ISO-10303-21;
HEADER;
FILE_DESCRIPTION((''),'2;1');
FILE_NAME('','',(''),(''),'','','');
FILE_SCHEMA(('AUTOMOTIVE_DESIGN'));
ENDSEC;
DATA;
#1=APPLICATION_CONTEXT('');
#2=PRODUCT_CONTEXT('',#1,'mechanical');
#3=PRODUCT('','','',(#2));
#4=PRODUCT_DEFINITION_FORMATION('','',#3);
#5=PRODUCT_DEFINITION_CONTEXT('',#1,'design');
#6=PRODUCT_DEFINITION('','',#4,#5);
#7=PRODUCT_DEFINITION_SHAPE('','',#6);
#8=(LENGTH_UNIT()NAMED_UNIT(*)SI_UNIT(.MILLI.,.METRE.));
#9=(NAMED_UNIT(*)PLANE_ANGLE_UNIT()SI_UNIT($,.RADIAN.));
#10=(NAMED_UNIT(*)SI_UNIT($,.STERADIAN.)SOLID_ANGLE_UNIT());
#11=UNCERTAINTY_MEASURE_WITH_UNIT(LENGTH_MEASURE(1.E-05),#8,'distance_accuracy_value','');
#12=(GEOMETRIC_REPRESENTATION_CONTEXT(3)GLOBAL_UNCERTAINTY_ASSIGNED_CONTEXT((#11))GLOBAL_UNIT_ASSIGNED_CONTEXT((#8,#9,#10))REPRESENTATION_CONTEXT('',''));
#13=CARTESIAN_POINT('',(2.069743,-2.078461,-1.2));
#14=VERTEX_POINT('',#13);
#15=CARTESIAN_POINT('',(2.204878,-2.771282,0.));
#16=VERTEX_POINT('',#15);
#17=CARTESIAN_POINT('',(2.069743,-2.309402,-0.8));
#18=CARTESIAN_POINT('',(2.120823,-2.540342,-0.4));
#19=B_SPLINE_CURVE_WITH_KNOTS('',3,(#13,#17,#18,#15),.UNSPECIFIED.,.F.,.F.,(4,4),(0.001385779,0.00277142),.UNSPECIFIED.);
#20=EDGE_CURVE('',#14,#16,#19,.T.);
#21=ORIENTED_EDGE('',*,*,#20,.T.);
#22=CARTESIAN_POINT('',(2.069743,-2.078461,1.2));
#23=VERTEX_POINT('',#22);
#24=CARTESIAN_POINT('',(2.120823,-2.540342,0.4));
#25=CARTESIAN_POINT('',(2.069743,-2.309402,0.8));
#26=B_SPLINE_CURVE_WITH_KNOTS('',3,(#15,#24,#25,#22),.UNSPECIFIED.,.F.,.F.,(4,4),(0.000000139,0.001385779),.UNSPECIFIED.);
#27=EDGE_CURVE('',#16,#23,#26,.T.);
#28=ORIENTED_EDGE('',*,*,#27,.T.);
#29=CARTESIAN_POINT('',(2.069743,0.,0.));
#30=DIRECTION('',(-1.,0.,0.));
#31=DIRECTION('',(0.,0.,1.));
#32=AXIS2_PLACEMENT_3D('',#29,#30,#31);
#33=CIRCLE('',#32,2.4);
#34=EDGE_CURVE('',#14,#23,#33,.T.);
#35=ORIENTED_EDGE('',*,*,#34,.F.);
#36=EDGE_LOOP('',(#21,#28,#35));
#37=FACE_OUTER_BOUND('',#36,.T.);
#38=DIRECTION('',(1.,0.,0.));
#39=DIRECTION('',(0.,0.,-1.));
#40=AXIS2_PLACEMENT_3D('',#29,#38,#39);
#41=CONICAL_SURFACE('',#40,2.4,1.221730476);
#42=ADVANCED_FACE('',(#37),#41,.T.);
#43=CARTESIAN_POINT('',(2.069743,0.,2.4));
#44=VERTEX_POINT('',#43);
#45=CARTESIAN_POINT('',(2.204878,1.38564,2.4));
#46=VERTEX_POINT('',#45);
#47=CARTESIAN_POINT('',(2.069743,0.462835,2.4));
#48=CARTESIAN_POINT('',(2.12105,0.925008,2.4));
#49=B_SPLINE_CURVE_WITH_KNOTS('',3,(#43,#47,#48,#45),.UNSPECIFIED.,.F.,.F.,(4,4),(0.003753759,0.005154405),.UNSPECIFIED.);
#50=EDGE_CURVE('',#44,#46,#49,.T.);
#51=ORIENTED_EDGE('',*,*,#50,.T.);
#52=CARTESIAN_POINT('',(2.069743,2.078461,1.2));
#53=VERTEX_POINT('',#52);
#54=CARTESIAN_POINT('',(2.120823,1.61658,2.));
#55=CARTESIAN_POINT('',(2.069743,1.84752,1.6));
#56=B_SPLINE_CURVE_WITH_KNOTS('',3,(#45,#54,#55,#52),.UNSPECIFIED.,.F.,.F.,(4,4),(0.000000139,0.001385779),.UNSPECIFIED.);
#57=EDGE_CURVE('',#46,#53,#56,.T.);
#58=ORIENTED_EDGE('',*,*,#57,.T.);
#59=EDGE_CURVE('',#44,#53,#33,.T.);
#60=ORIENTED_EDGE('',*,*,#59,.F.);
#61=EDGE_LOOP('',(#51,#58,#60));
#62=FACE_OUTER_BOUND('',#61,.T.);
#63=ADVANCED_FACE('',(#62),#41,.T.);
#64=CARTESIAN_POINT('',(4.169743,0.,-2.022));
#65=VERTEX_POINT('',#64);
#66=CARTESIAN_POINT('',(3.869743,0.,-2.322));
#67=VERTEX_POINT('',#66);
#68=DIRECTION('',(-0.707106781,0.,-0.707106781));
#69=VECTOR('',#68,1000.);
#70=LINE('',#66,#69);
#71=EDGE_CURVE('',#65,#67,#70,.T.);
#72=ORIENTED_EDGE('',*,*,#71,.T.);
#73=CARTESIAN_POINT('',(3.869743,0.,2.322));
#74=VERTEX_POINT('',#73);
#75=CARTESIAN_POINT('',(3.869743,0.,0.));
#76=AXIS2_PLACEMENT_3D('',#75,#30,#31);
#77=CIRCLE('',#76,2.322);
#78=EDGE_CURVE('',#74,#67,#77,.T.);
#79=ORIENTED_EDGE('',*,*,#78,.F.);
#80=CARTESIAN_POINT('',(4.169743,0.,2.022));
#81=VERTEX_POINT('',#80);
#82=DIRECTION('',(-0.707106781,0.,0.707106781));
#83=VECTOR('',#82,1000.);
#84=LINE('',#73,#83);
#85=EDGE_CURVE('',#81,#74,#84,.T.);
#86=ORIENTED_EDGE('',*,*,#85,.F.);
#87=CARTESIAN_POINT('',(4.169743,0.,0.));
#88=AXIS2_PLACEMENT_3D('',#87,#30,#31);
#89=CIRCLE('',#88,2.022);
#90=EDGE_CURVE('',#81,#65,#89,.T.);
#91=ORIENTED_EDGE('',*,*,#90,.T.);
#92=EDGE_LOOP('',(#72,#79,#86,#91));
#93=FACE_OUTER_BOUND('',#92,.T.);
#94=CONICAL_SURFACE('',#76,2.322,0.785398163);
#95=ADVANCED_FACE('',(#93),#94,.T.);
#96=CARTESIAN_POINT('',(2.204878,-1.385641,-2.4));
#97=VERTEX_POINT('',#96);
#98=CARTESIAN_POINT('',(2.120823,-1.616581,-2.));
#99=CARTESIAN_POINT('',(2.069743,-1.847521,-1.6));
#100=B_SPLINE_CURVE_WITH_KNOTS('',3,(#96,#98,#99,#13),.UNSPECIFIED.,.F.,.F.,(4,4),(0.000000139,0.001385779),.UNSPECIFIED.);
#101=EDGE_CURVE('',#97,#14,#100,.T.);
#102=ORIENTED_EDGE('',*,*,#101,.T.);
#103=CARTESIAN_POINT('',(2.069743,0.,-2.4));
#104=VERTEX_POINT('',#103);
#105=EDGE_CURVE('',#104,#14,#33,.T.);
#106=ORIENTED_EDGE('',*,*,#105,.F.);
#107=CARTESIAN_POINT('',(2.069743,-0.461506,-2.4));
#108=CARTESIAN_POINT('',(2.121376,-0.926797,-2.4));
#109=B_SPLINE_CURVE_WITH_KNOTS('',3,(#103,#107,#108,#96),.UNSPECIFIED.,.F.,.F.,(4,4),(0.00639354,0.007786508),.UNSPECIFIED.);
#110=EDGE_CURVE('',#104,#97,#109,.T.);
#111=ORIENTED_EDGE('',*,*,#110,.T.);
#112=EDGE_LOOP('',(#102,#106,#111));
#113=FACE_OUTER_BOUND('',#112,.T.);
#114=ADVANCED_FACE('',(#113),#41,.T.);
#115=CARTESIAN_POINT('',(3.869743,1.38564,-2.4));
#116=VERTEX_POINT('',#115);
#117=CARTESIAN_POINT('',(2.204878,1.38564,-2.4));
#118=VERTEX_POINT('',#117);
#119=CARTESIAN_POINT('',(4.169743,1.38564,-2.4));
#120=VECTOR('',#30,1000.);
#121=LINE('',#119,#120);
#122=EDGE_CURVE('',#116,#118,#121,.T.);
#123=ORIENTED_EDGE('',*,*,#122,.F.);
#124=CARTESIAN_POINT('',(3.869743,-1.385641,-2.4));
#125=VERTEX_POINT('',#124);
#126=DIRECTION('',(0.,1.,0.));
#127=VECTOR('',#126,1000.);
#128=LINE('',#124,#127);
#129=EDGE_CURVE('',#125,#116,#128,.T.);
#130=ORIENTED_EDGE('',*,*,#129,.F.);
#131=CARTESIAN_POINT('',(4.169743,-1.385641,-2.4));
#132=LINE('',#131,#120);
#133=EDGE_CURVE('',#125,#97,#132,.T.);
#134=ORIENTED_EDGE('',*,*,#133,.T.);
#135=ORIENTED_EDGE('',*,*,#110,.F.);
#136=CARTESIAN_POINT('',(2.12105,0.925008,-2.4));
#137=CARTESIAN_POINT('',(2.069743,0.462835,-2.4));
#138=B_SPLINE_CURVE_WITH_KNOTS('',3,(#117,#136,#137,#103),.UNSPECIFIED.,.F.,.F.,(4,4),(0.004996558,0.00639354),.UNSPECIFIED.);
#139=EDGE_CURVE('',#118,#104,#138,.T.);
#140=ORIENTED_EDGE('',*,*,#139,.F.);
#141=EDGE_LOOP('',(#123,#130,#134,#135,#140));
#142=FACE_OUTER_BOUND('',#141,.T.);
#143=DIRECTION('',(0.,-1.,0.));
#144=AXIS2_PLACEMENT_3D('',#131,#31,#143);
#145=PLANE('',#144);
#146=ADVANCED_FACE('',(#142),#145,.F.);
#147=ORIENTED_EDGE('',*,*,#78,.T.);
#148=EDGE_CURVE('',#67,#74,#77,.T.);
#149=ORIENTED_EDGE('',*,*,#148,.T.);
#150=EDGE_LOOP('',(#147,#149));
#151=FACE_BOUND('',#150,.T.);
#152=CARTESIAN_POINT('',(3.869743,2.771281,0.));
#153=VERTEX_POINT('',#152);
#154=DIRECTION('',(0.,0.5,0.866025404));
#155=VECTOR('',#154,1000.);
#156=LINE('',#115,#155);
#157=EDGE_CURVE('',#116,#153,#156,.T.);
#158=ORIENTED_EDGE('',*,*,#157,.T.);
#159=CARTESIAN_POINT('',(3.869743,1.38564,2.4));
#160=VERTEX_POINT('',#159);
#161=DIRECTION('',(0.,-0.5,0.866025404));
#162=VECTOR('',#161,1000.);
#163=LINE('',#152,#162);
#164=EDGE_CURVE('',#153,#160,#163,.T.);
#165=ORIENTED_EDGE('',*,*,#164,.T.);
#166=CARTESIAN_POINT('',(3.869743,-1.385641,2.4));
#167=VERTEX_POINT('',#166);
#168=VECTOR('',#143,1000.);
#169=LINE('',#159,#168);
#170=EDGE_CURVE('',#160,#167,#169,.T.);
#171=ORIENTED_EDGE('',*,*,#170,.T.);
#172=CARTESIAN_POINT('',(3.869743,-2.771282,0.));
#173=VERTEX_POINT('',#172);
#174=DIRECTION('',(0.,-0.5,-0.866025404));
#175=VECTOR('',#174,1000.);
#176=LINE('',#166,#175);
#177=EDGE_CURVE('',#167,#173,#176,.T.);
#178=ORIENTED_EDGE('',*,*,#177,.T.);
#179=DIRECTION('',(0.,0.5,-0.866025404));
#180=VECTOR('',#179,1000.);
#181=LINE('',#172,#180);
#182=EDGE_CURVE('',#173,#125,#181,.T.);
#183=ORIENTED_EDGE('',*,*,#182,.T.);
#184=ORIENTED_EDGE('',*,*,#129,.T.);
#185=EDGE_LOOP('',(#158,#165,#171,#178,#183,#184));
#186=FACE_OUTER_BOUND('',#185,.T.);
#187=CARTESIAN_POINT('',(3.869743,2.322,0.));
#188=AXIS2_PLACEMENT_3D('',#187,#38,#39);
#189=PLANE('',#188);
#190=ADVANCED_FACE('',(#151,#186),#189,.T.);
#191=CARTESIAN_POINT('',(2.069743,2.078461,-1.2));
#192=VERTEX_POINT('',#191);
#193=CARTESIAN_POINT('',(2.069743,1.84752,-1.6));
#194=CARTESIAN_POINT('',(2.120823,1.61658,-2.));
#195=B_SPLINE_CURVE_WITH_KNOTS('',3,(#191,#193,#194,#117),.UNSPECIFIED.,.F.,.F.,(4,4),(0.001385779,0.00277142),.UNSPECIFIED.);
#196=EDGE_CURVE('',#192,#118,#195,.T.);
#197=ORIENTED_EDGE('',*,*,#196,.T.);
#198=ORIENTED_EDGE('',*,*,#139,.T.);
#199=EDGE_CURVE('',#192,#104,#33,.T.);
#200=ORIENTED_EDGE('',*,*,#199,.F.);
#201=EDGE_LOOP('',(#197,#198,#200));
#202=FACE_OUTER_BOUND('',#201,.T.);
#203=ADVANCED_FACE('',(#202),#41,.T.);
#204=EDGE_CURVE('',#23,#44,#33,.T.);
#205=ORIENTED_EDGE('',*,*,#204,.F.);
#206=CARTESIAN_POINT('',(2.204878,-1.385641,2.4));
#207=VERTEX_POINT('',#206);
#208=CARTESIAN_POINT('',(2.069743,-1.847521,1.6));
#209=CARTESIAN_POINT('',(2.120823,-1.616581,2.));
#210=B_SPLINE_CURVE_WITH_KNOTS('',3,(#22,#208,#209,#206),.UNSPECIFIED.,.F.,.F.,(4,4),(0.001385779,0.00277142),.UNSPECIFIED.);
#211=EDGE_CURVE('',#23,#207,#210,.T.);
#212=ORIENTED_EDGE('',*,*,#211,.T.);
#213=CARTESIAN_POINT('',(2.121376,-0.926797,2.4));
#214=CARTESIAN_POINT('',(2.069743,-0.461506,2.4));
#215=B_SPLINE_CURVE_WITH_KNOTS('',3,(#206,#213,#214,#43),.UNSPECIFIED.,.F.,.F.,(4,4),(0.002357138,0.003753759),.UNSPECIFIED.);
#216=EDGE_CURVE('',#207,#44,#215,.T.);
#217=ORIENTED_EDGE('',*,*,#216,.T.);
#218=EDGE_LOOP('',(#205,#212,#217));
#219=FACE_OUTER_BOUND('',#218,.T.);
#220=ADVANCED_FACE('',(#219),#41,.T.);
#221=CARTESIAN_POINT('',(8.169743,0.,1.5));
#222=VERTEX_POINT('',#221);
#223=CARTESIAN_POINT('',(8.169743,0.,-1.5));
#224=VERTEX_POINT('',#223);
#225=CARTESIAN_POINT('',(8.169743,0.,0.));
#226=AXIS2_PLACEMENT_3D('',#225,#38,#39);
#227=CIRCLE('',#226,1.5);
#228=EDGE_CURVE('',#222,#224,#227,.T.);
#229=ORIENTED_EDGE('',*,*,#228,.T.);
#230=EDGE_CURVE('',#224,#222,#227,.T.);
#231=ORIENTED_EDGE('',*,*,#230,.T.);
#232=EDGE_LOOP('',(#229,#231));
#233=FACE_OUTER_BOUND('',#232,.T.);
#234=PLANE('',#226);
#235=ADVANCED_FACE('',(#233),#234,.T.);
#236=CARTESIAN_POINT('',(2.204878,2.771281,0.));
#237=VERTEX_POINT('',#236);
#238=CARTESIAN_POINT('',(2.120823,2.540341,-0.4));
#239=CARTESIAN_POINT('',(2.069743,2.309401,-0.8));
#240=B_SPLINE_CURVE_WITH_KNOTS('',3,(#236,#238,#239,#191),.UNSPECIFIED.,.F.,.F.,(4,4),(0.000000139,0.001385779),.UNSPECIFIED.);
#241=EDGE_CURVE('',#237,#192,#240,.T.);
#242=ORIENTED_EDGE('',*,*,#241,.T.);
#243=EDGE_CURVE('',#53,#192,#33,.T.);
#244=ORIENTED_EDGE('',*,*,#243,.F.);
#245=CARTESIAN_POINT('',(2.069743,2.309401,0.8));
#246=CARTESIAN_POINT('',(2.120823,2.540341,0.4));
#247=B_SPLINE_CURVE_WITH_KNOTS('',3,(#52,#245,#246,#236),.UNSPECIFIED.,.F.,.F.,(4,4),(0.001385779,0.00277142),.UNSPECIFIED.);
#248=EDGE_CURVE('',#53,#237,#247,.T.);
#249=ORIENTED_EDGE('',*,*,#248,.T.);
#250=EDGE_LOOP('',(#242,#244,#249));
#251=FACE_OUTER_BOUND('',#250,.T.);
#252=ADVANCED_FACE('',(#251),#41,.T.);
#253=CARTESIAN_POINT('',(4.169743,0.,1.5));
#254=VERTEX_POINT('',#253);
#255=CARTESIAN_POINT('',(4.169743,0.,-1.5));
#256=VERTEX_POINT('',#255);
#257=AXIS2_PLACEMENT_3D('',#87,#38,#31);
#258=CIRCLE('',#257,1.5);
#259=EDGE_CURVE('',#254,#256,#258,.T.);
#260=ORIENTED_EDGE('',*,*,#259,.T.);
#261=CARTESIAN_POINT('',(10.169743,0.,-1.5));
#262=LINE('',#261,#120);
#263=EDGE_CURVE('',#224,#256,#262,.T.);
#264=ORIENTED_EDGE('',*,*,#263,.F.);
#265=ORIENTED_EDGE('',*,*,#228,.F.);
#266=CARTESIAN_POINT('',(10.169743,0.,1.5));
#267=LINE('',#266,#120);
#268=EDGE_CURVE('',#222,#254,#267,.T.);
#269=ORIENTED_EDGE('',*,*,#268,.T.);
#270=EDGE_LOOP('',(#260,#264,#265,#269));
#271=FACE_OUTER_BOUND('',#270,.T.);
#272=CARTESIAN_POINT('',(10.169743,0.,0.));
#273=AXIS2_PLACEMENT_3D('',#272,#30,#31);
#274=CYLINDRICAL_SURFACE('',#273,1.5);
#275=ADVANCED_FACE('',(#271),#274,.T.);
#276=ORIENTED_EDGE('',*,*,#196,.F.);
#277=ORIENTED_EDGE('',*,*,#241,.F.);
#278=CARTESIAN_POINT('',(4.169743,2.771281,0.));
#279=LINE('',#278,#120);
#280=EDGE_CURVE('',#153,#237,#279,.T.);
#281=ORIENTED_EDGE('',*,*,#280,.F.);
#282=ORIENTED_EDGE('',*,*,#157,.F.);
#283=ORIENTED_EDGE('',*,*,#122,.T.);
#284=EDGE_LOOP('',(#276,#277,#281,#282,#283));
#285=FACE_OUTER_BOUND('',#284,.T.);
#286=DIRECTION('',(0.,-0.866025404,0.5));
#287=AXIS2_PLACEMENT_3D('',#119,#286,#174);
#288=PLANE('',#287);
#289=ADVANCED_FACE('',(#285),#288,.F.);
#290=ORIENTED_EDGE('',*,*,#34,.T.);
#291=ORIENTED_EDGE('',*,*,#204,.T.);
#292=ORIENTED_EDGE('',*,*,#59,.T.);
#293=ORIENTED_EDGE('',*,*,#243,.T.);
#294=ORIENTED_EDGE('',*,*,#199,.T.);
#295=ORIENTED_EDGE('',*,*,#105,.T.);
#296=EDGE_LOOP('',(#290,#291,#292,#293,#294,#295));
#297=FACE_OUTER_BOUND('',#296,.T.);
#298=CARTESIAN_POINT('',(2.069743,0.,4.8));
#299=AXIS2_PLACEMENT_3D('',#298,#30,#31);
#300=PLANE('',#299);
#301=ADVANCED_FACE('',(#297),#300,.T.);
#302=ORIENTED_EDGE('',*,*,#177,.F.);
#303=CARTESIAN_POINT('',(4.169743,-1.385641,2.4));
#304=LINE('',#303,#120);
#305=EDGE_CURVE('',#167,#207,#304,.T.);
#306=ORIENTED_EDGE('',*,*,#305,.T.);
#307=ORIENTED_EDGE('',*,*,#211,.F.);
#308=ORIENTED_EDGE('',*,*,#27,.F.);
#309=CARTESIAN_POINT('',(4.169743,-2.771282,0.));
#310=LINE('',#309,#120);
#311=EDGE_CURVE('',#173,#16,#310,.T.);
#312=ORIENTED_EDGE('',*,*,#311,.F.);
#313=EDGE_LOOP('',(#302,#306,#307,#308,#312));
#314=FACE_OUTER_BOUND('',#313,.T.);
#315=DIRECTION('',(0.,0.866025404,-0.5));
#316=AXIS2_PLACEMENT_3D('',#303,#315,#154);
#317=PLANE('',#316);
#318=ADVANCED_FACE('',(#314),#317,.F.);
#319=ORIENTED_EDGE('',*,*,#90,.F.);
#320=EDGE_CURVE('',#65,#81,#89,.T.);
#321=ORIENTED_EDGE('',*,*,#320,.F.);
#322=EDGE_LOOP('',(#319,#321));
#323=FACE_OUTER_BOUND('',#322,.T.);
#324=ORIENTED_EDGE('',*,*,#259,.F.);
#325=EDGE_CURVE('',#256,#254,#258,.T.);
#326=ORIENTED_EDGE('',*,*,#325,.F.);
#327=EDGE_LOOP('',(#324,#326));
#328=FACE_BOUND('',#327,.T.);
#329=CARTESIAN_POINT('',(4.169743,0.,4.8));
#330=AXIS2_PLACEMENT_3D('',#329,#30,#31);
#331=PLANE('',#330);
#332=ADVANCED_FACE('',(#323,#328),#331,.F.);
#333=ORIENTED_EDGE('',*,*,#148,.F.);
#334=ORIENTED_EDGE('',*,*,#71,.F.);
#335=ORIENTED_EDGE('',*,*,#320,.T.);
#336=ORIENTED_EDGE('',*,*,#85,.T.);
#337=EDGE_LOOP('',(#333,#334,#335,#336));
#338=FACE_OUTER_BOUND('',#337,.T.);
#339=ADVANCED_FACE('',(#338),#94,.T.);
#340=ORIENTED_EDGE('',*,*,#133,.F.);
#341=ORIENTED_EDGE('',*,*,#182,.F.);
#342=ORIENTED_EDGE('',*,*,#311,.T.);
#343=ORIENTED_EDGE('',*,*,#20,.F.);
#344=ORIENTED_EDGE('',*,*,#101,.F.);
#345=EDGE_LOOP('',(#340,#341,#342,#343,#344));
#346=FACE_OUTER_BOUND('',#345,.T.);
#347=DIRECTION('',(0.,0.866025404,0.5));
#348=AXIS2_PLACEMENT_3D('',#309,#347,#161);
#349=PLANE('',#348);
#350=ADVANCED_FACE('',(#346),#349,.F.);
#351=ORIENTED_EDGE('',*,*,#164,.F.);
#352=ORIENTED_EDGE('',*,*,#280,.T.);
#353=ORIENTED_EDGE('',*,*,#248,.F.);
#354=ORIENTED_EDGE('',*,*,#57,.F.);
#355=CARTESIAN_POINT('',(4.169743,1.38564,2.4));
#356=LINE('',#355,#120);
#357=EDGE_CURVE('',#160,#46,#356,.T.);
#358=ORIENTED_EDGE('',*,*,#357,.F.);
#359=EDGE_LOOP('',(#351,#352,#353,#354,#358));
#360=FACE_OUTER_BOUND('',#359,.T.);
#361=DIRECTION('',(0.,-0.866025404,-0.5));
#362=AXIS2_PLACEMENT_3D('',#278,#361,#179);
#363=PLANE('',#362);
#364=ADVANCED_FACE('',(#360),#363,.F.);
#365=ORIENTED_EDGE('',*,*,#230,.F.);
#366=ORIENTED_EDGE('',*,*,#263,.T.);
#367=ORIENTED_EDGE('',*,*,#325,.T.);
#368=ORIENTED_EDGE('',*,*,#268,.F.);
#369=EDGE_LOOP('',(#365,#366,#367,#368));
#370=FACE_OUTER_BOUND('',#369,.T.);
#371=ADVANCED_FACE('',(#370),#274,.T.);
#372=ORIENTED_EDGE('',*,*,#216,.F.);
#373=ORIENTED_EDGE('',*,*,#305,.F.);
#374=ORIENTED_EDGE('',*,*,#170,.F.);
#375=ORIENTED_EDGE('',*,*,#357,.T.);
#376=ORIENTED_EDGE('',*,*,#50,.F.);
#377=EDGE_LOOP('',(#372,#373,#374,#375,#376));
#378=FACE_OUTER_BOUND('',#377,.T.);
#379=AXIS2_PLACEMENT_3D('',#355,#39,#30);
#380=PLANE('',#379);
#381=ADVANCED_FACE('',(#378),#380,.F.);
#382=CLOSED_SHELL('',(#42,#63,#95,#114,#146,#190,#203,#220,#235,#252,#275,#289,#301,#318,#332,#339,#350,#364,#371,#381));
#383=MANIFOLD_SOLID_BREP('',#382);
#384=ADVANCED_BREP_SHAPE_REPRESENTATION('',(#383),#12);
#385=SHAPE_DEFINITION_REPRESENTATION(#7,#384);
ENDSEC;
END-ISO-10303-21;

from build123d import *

# Parameters (mm, degrees)
BASEHEAD_DEPTH     = 3.5
SKETCH5_R          = 2.5
BASEBODY_DEPTH     = 10
CHAMFER1_SIZE      = 0.25
SCALE1_SCALE       = 0.6
SKETCH1_R          = 1.918221386
CUT_EXTRUDE1_DEPTH = 2


with BuildPart() as part:
    # Sketch2 → BaseHead (new body)
    with BuildSketch(Plane(origin=(0, 0, 0), x_dir=(0, 0, -1), z_dir=(1, 0, 0))):
        Polygon((0, -4.618802154), (4, -2.309401077), (4, 2.309401077), (0, 4.618802154), (-4, 2.309401077), (-4, -2.309401077), align=None)
    extrude(amount=BASEHEAD_DEPTH)

    # Sketch3 → BearingFace (revolve, cut)
    with BuildSketch(Plane.XY, mode=Mode.PRIVATE) as bearingface_sk:
        Polygon((3.5, 4.618802154), (3.5, 3.37), (3, 3.87), (3, 4.618802154), align=None)
    revolve(bearingface_sk.sketch.rotate(Axis((-0.957090588, 0, 0), (1, 0, 0)), 90), axis=Axis((-0.957090588, 0, 0), (1, 0, 0)), mode=Mode.SUBTRACT)

    # Sketch4 → HeadChamfer (revolve, cut)
    with BuildSketch(Plane.XY):
        Polygon((0, 4.618802154), (0.225225565, 4.618802154), (0, 4), align=None)
    revolve(axis=Axis((-0.493528746, 0, 0), (1, 0, 0)), mode=Mode.SUBTRACT)

    # Sketch5 → BaseBody (add)
    with BuildSketch(Plane(origin=(3.5, 0, 0), x_dir=(0, 0, -1), z_dir=(1, 0, 0))):
        with Locations(Location((0, 0, 0), (0, 0, 180))):
            Circle(SKETCH5_R)
    extrude(amount=BASEBODY_DEPTH)

    # Chamfer1
    chamfer1_edges = [part.edges().sort_by_distance(p)[0] for p in [
        (13.5, 0, -2.5),
    ]]
    chamfer(chamfer1_edges, length=CHAMFER1_SIZE)


with BuildPart() as part_1:
    # Scale1: scaled about (5.174356306, 0, 0)
    add(part.part.scale(SCALE1_SCALE).moved(Location((2.069742522, 0, 0))))

    # Sketch1 → Cut-Extrude1 (cut)
    with BuildSketch(Plane(origin=(10.169743001, 0, 0), x_dir=(0, 0, -1), z_dir=(1, 0, 0))):
        Circle(SKETCH1_R)
    extrude(amount=-CUT_EXTRUDE1_DEPTH, mode=Mode.SUBTRACT)


solid = part_1.part
